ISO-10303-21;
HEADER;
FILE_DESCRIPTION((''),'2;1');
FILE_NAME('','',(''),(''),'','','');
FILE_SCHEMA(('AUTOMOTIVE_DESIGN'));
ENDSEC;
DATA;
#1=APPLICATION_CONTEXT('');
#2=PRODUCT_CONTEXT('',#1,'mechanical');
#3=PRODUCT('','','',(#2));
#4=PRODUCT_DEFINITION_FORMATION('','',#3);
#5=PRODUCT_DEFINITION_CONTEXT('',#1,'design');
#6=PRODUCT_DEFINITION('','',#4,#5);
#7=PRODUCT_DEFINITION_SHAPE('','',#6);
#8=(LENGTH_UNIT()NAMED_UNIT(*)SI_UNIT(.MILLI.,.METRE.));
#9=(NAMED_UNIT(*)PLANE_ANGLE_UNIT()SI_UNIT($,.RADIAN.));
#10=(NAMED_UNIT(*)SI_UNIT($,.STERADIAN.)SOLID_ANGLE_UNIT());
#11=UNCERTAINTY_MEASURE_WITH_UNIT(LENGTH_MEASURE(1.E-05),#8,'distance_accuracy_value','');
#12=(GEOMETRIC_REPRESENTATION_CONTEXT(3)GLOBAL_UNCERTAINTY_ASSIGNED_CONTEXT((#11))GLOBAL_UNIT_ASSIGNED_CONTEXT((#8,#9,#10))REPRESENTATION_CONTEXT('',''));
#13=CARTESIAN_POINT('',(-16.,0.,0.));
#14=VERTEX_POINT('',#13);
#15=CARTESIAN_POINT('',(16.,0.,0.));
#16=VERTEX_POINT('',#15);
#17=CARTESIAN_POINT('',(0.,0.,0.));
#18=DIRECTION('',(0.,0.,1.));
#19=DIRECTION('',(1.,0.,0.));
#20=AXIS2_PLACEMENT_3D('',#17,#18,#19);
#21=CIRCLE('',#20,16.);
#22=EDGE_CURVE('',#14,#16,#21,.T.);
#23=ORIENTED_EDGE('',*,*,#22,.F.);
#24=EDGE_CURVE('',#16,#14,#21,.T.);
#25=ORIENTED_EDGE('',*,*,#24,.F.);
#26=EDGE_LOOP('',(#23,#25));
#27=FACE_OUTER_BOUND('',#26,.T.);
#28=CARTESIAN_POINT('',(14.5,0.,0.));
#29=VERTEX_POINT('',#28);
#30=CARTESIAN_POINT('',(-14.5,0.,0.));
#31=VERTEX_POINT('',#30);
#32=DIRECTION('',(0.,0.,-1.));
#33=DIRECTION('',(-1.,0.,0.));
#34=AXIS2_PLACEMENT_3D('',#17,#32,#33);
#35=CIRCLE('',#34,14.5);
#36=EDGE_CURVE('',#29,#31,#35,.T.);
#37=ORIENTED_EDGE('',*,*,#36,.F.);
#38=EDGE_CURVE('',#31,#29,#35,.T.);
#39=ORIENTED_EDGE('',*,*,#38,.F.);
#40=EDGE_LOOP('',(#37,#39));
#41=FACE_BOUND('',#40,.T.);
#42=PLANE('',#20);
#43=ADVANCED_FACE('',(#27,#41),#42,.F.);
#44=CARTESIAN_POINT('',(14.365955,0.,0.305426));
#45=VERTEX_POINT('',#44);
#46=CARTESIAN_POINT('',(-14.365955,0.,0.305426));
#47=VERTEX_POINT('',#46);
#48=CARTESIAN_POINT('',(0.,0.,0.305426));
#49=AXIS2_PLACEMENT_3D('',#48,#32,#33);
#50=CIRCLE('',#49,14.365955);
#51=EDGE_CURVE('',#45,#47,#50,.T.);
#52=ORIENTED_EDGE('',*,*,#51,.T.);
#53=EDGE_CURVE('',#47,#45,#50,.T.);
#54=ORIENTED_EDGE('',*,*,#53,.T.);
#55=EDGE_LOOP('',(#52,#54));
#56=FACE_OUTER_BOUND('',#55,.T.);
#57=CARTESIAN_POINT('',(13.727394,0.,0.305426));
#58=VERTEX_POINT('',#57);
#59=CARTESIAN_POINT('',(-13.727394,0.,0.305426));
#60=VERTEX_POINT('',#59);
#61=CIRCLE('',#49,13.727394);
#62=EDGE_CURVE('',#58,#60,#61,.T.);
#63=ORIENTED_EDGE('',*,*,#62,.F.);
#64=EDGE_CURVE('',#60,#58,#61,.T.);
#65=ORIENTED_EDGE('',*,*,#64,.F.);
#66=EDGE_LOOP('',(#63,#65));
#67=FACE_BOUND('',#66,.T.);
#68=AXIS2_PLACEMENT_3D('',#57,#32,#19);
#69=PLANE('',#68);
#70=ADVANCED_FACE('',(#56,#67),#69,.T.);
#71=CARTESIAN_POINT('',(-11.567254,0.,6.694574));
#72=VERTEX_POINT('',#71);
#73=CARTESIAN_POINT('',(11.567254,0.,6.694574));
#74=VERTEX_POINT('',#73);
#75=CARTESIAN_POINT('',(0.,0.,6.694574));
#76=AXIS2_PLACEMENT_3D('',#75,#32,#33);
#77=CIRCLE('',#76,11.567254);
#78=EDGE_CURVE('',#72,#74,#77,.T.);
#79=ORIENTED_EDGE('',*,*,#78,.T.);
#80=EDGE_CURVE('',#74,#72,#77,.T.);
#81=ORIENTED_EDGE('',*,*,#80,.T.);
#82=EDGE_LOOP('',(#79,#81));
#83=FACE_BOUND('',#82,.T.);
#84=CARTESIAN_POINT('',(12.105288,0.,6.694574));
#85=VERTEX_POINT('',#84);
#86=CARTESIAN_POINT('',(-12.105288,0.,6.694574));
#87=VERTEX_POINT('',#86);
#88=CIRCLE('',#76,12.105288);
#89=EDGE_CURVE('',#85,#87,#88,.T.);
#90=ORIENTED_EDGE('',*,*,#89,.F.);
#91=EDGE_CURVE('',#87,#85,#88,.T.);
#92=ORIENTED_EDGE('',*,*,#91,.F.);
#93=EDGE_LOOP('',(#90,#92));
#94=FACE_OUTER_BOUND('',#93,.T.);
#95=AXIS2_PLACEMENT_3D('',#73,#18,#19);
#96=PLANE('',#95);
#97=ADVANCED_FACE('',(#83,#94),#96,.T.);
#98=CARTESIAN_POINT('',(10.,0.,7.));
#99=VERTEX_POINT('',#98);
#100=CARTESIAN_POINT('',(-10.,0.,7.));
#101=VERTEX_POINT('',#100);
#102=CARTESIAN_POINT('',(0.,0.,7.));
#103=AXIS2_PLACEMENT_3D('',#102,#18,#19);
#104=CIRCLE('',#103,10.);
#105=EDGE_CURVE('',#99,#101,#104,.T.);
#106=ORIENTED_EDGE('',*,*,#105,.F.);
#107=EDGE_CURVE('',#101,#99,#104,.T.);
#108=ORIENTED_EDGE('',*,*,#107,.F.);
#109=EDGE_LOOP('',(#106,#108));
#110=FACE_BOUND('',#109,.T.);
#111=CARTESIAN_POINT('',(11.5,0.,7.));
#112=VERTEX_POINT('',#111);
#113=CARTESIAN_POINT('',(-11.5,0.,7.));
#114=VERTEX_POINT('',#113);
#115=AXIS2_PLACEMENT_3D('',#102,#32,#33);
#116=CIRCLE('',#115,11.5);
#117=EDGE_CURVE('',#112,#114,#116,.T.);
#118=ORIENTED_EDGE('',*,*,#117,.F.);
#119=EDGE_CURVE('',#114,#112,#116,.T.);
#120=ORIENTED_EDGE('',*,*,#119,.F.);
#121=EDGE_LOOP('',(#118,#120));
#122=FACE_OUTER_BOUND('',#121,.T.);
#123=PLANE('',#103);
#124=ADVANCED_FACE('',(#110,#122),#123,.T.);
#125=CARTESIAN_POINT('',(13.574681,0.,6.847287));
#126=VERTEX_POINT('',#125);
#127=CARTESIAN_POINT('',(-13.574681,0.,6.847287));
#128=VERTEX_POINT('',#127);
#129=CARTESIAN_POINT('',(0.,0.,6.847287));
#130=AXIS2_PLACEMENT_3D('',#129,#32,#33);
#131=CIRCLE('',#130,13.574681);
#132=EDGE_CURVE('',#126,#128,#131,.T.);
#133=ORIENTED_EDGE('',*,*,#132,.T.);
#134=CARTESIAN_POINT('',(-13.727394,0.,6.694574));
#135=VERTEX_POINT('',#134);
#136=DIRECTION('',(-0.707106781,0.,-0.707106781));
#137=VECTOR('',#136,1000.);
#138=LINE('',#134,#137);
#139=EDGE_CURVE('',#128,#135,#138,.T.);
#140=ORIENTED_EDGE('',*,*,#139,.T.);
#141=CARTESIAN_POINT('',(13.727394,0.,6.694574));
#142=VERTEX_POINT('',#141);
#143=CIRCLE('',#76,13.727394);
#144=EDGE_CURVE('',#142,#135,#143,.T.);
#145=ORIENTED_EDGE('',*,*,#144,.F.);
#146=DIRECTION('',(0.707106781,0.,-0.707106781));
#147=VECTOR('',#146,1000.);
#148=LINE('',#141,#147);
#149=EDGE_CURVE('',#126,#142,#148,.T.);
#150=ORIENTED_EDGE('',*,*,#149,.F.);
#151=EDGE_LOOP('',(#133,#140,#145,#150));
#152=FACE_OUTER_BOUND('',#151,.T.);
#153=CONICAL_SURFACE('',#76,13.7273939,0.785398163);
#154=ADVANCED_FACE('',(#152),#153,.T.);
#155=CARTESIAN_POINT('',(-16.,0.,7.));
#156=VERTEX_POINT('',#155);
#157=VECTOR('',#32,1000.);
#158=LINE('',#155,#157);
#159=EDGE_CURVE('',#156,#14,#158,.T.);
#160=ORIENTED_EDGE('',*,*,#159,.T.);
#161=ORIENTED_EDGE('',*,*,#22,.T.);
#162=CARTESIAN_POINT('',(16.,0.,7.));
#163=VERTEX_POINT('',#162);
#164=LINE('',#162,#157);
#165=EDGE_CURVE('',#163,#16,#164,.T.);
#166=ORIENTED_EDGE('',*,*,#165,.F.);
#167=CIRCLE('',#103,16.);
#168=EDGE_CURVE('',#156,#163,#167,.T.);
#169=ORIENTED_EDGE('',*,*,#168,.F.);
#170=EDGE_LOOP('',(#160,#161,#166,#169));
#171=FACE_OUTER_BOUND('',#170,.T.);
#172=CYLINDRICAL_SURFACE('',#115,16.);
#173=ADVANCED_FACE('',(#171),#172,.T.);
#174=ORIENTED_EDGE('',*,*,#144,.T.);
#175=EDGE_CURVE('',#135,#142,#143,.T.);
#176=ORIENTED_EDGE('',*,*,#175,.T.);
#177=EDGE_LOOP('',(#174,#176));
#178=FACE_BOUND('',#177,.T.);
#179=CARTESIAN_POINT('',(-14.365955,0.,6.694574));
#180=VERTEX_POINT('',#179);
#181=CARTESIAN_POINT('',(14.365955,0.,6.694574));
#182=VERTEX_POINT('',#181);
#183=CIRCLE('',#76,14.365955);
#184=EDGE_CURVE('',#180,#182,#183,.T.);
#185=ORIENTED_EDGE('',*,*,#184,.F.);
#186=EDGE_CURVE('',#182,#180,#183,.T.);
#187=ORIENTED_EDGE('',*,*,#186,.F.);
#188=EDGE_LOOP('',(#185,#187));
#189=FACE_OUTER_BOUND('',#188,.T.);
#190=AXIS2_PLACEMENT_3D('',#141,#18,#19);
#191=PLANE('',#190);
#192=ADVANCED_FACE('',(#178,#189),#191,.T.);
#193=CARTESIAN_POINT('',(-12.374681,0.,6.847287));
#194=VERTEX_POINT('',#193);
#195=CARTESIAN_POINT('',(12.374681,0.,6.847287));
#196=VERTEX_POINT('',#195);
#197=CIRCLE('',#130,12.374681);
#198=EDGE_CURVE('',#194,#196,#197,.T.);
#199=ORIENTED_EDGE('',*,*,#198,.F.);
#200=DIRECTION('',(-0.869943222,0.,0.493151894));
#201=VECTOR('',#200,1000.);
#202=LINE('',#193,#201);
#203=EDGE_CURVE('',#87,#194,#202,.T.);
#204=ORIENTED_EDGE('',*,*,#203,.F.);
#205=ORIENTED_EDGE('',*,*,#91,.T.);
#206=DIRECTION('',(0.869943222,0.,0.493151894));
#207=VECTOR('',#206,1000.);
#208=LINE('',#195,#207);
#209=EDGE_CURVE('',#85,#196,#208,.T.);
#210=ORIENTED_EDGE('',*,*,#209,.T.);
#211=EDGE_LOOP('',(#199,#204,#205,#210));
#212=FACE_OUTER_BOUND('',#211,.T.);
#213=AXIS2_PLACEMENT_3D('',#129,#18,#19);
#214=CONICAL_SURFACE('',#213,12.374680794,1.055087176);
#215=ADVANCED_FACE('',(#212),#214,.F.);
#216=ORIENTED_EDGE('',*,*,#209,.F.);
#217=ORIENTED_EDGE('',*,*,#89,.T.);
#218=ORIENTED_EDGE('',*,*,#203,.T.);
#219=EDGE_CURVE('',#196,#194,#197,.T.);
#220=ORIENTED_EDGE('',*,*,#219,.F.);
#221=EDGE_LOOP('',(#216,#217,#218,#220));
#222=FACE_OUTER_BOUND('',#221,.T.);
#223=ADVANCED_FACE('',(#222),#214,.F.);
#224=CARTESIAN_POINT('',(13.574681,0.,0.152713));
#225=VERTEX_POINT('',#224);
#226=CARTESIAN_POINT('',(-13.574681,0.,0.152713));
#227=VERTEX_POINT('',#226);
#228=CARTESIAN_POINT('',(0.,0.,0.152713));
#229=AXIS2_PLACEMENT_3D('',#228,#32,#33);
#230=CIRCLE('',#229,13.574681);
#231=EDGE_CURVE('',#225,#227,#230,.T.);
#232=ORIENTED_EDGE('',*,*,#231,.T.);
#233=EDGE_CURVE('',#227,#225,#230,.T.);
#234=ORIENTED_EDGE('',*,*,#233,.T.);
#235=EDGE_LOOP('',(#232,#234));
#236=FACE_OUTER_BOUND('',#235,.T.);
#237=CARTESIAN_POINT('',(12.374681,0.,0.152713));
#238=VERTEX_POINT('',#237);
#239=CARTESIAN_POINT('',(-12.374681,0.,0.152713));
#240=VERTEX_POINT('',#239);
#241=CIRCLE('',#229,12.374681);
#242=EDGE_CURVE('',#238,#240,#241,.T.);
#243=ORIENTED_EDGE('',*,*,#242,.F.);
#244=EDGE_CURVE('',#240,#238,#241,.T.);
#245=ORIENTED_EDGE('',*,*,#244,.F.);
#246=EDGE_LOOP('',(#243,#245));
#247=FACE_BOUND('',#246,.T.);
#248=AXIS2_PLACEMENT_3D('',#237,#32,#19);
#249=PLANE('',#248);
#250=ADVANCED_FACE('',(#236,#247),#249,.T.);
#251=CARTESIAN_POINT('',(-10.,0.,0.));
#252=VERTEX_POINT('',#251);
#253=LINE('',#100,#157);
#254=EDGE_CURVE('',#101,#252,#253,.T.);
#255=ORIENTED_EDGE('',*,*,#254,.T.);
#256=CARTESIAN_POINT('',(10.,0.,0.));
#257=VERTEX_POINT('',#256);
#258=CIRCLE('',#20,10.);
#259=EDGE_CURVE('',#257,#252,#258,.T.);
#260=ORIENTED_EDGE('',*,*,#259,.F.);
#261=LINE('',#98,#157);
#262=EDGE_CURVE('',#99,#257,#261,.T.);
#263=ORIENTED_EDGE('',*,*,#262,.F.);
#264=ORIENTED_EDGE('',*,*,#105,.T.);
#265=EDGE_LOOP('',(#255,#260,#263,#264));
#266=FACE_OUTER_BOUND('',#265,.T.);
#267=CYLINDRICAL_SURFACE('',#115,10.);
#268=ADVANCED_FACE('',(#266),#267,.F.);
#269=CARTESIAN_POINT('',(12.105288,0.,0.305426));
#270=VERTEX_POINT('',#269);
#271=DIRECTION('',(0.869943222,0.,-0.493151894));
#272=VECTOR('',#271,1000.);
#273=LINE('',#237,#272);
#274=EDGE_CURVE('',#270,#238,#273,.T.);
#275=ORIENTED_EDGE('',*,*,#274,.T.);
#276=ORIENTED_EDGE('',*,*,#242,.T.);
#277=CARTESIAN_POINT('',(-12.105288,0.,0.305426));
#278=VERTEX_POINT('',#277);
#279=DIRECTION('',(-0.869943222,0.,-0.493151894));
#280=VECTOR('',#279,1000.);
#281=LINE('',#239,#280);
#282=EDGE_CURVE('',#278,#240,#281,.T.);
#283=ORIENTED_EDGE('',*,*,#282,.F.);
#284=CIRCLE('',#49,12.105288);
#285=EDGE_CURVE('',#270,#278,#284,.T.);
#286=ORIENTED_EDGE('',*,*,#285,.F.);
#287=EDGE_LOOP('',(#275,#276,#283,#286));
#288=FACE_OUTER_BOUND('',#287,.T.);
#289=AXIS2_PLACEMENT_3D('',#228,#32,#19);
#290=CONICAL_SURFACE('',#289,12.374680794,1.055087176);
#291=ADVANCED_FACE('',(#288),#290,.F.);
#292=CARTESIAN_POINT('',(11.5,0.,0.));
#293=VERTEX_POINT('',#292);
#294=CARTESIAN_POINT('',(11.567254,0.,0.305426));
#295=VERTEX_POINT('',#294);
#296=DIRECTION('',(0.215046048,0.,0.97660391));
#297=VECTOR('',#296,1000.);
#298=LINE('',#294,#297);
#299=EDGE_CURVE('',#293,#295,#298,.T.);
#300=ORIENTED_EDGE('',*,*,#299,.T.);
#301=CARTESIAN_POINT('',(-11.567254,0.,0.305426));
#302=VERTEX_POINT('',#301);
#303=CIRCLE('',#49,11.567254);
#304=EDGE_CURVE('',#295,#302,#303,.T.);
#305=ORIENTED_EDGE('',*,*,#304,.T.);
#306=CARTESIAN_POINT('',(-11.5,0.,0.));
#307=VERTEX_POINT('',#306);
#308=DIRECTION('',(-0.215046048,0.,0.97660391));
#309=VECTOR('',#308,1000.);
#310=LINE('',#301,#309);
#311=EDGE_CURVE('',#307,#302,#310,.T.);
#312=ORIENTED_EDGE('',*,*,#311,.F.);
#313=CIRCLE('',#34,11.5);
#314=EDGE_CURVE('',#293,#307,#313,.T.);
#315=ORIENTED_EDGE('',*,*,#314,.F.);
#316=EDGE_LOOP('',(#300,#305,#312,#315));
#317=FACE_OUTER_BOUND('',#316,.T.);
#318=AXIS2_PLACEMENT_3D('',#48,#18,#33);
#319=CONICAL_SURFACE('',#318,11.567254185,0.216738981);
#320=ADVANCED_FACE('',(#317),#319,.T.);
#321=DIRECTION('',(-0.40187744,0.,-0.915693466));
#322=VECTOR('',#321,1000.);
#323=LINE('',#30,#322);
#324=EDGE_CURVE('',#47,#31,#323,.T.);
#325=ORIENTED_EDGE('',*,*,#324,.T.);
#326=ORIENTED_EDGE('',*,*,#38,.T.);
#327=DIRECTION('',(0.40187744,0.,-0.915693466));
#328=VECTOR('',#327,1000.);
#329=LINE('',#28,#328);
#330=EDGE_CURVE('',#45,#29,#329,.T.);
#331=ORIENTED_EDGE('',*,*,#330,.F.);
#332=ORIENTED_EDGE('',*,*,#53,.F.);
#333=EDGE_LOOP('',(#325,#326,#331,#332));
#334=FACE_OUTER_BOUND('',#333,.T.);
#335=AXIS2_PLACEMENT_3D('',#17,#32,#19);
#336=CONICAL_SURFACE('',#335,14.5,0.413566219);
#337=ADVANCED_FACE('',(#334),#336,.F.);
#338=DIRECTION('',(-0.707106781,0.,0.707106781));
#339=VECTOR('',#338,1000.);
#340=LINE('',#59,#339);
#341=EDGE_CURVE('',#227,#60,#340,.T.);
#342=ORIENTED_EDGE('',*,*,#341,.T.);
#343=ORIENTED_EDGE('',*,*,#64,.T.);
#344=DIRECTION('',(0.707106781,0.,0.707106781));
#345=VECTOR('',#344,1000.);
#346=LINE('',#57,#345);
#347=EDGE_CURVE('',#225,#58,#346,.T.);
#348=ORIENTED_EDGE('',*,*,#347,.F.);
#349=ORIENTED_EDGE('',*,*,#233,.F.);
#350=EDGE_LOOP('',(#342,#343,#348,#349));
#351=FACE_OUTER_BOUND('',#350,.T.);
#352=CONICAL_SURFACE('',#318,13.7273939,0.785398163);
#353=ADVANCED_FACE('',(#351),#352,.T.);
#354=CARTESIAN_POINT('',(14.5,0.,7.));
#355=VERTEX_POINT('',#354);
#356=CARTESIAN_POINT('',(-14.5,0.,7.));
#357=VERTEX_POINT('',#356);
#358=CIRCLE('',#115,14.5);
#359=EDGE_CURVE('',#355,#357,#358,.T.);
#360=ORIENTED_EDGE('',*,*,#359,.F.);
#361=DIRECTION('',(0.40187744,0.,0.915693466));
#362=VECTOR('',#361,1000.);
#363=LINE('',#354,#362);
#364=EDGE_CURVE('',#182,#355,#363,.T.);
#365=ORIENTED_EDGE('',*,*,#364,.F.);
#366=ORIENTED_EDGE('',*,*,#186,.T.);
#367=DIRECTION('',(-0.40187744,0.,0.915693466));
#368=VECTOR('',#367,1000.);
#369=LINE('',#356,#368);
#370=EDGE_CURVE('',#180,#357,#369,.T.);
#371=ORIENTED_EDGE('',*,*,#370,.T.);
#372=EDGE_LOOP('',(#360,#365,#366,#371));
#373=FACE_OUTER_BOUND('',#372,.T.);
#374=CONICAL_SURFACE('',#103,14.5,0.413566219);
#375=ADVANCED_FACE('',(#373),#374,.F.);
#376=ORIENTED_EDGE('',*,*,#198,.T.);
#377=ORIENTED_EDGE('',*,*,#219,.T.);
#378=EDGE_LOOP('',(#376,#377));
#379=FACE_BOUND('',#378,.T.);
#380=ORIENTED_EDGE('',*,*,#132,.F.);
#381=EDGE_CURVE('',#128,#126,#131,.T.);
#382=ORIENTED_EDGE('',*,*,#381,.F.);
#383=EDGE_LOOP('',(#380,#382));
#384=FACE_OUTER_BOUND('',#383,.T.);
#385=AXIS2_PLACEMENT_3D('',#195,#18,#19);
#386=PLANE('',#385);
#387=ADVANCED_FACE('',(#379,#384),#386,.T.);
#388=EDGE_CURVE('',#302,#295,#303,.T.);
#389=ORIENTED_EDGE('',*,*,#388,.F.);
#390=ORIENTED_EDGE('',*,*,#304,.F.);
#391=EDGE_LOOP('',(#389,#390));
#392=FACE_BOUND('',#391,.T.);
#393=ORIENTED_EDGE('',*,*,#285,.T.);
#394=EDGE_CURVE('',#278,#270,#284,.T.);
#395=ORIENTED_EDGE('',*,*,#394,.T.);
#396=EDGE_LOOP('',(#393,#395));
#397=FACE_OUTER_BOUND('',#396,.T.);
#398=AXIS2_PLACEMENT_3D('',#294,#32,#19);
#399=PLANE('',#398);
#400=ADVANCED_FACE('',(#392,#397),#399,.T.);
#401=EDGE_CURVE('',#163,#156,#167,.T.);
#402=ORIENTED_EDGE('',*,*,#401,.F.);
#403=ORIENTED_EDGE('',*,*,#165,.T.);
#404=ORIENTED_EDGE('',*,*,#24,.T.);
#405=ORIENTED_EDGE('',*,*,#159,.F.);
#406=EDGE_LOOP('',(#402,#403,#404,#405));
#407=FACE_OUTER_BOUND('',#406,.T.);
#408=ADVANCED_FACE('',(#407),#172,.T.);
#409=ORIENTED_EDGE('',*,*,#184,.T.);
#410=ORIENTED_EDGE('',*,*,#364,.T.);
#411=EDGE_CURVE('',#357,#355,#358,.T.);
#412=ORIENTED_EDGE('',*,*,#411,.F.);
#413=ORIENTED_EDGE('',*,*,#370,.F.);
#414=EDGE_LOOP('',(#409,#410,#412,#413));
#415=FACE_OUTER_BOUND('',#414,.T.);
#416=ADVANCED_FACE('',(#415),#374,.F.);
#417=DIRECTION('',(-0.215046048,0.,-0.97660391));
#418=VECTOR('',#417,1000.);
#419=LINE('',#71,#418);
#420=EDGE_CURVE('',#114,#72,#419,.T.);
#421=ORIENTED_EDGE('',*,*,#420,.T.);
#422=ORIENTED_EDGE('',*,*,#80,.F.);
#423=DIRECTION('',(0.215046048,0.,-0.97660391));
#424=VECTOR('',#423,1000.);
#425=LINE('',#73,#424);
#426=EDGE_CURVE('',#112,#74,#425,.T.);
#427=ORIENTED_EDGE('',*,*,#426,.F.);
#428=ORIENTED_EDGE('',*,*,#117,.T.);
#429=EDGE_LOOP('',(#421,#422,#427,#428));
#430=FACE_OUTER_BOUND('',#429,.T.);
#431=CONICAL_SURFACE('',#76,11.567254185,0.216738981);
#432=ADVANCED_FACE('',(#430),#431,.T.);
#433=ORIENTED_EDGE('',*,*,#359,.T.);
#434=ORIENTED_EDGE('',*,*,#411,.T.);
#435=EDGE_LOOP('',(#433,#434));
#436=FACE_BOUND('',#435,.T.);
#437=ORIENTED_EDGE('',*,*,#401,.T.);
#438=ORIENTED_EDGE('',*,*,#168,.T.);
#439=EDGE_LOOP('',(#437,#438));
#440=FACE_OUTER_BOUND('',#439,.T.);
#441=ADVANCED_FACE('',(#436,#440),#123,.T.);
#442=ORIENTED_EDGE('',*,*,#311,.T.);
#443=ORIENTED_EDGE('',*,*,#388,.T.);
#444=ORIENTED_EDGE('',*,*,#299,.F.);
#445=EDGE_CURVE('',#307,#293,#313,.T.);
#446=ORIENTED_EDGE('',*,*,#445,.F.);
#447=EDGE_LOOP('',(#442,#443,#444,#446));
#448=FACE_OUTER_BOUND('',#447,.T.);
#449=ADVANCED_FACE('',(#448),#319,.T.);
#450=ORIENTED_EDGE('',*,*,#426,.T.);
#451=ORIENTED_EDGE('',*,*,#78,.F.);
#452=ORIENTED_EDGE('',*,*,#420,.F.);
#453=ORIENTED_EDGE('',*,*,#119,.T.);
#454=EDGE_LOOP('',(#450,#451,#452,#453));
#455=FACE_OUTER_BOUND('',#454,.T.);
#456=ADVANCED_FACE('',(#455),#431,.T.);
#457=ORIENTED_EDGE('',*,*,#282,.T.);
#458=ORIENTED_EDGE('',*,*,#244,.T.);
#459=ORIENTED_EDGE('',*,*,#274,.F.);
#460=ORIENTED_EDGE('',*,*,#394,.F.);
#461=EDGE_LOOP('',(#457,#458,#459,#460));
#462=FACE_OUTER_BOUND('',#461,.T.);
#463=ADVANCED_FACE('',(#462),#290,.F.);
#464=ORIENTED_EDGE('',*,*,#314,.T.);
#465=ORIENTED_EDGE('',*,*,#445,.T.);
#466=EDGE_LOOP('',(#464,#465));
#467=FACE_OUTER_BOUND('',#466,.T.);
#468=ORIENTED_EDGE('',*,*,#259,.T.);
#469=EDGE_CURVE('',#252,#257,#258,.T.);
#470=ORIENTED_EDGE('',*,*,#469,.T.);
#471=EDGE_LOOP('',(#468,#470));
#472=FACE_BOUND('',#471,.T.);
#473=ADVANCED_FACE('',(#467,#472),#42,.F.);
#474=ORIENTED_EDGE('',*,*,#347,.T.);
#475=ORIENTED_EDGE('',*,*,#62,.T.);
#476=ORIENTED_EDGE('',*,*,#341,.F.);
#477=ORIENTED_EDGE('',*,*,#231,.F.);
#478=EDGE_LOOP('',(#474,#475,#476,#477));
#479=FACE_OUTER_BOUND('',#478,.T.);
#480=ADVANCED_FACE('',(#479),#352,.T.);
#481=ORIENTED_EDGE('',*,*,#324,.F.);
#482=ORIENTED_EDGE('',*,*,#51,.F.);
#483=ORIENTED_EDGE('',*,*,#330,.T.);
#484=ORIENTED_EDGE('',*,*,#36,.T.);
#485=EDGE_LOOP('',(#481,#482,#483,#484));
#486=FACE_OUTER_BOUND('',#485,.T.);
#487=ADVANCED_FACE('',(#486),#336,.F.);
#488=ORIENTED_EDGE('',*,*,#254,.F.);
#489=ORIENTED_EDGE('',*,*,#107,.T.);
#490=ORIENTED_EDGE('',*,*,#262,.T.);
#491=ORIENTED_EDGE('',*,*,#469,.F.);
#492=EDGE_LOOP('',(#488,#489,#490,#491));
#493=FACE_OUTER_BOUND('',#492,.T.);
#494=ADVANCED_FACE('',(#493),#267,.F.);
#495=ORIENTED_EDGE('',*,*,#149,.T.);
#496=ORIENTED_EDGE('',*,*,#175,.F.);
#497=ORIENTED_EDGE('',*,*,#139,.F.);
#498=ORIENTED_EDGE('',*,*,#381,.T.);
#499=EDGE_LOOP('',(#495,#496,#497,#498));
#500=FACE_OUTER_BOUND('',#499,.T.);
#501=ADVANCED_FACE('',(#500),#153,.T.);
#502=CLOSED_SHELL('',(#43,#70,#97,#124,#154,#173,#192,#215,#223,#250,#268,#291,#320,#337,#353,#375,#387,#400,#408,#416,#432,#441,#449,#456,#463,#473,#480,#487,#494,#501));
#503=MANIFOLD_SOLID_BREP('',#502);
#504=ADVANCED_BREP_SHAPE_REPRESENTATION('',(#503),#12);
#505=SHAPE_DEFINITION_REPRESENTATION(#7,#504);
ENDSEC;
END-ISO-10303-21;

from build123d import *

# Parameters (mm, degrees)
SKETCH1_R           = 16
SKETCH1_R_2         = 10
BOSS_EXTRUDE1_DEPTH = 7


with BuildPart() as part:
    # Sketch1 → Boss-Extrude1 (new body)
    with BuildSketch(Plane.XY):
        Circle(SKETCH1_R)
        Circle(SKETCH1_R_2, mode=Mode.SUBTRACT)
    extrude(amount=BOSS_EXTRUDE1_DEPTH)

    # Sketch3 → Cut-Revolve1 (revolve, cut)
    with BuildSketch(Plane(origin=(0, 0, 0), x_dir=(1, 0, 0), z_dir=(0, 1, 0)), mode=Mode.PRIVATE) as cut_revolve1_sk:
        Polygon((11.5, -7), (11.567254185, -6.694573787), (12.105287665, -6.694573787), (12.374680794, -6.847286894), (13.574680794, -6.847286894), (13.7273939, -6.694573787), (14.365955247, -6.694573787), (14.5, -7), align=None)
    cut_revolve1 = revolve(cut_revolve1_sk.sketch.rotate(Axis((0, 0, 0), (0, 0, 1)), 180), axis=Axis((0, 0, 0), (0, 0, 1)), mode=Mode.SUBTRACT)

    # Mirror1: Cut-Revolve1 across plane
    add(cut_revolve1.mirror(Plane.XY.offset(3.5)), mode=Mode.SUBTRACT)


solid = part.part
